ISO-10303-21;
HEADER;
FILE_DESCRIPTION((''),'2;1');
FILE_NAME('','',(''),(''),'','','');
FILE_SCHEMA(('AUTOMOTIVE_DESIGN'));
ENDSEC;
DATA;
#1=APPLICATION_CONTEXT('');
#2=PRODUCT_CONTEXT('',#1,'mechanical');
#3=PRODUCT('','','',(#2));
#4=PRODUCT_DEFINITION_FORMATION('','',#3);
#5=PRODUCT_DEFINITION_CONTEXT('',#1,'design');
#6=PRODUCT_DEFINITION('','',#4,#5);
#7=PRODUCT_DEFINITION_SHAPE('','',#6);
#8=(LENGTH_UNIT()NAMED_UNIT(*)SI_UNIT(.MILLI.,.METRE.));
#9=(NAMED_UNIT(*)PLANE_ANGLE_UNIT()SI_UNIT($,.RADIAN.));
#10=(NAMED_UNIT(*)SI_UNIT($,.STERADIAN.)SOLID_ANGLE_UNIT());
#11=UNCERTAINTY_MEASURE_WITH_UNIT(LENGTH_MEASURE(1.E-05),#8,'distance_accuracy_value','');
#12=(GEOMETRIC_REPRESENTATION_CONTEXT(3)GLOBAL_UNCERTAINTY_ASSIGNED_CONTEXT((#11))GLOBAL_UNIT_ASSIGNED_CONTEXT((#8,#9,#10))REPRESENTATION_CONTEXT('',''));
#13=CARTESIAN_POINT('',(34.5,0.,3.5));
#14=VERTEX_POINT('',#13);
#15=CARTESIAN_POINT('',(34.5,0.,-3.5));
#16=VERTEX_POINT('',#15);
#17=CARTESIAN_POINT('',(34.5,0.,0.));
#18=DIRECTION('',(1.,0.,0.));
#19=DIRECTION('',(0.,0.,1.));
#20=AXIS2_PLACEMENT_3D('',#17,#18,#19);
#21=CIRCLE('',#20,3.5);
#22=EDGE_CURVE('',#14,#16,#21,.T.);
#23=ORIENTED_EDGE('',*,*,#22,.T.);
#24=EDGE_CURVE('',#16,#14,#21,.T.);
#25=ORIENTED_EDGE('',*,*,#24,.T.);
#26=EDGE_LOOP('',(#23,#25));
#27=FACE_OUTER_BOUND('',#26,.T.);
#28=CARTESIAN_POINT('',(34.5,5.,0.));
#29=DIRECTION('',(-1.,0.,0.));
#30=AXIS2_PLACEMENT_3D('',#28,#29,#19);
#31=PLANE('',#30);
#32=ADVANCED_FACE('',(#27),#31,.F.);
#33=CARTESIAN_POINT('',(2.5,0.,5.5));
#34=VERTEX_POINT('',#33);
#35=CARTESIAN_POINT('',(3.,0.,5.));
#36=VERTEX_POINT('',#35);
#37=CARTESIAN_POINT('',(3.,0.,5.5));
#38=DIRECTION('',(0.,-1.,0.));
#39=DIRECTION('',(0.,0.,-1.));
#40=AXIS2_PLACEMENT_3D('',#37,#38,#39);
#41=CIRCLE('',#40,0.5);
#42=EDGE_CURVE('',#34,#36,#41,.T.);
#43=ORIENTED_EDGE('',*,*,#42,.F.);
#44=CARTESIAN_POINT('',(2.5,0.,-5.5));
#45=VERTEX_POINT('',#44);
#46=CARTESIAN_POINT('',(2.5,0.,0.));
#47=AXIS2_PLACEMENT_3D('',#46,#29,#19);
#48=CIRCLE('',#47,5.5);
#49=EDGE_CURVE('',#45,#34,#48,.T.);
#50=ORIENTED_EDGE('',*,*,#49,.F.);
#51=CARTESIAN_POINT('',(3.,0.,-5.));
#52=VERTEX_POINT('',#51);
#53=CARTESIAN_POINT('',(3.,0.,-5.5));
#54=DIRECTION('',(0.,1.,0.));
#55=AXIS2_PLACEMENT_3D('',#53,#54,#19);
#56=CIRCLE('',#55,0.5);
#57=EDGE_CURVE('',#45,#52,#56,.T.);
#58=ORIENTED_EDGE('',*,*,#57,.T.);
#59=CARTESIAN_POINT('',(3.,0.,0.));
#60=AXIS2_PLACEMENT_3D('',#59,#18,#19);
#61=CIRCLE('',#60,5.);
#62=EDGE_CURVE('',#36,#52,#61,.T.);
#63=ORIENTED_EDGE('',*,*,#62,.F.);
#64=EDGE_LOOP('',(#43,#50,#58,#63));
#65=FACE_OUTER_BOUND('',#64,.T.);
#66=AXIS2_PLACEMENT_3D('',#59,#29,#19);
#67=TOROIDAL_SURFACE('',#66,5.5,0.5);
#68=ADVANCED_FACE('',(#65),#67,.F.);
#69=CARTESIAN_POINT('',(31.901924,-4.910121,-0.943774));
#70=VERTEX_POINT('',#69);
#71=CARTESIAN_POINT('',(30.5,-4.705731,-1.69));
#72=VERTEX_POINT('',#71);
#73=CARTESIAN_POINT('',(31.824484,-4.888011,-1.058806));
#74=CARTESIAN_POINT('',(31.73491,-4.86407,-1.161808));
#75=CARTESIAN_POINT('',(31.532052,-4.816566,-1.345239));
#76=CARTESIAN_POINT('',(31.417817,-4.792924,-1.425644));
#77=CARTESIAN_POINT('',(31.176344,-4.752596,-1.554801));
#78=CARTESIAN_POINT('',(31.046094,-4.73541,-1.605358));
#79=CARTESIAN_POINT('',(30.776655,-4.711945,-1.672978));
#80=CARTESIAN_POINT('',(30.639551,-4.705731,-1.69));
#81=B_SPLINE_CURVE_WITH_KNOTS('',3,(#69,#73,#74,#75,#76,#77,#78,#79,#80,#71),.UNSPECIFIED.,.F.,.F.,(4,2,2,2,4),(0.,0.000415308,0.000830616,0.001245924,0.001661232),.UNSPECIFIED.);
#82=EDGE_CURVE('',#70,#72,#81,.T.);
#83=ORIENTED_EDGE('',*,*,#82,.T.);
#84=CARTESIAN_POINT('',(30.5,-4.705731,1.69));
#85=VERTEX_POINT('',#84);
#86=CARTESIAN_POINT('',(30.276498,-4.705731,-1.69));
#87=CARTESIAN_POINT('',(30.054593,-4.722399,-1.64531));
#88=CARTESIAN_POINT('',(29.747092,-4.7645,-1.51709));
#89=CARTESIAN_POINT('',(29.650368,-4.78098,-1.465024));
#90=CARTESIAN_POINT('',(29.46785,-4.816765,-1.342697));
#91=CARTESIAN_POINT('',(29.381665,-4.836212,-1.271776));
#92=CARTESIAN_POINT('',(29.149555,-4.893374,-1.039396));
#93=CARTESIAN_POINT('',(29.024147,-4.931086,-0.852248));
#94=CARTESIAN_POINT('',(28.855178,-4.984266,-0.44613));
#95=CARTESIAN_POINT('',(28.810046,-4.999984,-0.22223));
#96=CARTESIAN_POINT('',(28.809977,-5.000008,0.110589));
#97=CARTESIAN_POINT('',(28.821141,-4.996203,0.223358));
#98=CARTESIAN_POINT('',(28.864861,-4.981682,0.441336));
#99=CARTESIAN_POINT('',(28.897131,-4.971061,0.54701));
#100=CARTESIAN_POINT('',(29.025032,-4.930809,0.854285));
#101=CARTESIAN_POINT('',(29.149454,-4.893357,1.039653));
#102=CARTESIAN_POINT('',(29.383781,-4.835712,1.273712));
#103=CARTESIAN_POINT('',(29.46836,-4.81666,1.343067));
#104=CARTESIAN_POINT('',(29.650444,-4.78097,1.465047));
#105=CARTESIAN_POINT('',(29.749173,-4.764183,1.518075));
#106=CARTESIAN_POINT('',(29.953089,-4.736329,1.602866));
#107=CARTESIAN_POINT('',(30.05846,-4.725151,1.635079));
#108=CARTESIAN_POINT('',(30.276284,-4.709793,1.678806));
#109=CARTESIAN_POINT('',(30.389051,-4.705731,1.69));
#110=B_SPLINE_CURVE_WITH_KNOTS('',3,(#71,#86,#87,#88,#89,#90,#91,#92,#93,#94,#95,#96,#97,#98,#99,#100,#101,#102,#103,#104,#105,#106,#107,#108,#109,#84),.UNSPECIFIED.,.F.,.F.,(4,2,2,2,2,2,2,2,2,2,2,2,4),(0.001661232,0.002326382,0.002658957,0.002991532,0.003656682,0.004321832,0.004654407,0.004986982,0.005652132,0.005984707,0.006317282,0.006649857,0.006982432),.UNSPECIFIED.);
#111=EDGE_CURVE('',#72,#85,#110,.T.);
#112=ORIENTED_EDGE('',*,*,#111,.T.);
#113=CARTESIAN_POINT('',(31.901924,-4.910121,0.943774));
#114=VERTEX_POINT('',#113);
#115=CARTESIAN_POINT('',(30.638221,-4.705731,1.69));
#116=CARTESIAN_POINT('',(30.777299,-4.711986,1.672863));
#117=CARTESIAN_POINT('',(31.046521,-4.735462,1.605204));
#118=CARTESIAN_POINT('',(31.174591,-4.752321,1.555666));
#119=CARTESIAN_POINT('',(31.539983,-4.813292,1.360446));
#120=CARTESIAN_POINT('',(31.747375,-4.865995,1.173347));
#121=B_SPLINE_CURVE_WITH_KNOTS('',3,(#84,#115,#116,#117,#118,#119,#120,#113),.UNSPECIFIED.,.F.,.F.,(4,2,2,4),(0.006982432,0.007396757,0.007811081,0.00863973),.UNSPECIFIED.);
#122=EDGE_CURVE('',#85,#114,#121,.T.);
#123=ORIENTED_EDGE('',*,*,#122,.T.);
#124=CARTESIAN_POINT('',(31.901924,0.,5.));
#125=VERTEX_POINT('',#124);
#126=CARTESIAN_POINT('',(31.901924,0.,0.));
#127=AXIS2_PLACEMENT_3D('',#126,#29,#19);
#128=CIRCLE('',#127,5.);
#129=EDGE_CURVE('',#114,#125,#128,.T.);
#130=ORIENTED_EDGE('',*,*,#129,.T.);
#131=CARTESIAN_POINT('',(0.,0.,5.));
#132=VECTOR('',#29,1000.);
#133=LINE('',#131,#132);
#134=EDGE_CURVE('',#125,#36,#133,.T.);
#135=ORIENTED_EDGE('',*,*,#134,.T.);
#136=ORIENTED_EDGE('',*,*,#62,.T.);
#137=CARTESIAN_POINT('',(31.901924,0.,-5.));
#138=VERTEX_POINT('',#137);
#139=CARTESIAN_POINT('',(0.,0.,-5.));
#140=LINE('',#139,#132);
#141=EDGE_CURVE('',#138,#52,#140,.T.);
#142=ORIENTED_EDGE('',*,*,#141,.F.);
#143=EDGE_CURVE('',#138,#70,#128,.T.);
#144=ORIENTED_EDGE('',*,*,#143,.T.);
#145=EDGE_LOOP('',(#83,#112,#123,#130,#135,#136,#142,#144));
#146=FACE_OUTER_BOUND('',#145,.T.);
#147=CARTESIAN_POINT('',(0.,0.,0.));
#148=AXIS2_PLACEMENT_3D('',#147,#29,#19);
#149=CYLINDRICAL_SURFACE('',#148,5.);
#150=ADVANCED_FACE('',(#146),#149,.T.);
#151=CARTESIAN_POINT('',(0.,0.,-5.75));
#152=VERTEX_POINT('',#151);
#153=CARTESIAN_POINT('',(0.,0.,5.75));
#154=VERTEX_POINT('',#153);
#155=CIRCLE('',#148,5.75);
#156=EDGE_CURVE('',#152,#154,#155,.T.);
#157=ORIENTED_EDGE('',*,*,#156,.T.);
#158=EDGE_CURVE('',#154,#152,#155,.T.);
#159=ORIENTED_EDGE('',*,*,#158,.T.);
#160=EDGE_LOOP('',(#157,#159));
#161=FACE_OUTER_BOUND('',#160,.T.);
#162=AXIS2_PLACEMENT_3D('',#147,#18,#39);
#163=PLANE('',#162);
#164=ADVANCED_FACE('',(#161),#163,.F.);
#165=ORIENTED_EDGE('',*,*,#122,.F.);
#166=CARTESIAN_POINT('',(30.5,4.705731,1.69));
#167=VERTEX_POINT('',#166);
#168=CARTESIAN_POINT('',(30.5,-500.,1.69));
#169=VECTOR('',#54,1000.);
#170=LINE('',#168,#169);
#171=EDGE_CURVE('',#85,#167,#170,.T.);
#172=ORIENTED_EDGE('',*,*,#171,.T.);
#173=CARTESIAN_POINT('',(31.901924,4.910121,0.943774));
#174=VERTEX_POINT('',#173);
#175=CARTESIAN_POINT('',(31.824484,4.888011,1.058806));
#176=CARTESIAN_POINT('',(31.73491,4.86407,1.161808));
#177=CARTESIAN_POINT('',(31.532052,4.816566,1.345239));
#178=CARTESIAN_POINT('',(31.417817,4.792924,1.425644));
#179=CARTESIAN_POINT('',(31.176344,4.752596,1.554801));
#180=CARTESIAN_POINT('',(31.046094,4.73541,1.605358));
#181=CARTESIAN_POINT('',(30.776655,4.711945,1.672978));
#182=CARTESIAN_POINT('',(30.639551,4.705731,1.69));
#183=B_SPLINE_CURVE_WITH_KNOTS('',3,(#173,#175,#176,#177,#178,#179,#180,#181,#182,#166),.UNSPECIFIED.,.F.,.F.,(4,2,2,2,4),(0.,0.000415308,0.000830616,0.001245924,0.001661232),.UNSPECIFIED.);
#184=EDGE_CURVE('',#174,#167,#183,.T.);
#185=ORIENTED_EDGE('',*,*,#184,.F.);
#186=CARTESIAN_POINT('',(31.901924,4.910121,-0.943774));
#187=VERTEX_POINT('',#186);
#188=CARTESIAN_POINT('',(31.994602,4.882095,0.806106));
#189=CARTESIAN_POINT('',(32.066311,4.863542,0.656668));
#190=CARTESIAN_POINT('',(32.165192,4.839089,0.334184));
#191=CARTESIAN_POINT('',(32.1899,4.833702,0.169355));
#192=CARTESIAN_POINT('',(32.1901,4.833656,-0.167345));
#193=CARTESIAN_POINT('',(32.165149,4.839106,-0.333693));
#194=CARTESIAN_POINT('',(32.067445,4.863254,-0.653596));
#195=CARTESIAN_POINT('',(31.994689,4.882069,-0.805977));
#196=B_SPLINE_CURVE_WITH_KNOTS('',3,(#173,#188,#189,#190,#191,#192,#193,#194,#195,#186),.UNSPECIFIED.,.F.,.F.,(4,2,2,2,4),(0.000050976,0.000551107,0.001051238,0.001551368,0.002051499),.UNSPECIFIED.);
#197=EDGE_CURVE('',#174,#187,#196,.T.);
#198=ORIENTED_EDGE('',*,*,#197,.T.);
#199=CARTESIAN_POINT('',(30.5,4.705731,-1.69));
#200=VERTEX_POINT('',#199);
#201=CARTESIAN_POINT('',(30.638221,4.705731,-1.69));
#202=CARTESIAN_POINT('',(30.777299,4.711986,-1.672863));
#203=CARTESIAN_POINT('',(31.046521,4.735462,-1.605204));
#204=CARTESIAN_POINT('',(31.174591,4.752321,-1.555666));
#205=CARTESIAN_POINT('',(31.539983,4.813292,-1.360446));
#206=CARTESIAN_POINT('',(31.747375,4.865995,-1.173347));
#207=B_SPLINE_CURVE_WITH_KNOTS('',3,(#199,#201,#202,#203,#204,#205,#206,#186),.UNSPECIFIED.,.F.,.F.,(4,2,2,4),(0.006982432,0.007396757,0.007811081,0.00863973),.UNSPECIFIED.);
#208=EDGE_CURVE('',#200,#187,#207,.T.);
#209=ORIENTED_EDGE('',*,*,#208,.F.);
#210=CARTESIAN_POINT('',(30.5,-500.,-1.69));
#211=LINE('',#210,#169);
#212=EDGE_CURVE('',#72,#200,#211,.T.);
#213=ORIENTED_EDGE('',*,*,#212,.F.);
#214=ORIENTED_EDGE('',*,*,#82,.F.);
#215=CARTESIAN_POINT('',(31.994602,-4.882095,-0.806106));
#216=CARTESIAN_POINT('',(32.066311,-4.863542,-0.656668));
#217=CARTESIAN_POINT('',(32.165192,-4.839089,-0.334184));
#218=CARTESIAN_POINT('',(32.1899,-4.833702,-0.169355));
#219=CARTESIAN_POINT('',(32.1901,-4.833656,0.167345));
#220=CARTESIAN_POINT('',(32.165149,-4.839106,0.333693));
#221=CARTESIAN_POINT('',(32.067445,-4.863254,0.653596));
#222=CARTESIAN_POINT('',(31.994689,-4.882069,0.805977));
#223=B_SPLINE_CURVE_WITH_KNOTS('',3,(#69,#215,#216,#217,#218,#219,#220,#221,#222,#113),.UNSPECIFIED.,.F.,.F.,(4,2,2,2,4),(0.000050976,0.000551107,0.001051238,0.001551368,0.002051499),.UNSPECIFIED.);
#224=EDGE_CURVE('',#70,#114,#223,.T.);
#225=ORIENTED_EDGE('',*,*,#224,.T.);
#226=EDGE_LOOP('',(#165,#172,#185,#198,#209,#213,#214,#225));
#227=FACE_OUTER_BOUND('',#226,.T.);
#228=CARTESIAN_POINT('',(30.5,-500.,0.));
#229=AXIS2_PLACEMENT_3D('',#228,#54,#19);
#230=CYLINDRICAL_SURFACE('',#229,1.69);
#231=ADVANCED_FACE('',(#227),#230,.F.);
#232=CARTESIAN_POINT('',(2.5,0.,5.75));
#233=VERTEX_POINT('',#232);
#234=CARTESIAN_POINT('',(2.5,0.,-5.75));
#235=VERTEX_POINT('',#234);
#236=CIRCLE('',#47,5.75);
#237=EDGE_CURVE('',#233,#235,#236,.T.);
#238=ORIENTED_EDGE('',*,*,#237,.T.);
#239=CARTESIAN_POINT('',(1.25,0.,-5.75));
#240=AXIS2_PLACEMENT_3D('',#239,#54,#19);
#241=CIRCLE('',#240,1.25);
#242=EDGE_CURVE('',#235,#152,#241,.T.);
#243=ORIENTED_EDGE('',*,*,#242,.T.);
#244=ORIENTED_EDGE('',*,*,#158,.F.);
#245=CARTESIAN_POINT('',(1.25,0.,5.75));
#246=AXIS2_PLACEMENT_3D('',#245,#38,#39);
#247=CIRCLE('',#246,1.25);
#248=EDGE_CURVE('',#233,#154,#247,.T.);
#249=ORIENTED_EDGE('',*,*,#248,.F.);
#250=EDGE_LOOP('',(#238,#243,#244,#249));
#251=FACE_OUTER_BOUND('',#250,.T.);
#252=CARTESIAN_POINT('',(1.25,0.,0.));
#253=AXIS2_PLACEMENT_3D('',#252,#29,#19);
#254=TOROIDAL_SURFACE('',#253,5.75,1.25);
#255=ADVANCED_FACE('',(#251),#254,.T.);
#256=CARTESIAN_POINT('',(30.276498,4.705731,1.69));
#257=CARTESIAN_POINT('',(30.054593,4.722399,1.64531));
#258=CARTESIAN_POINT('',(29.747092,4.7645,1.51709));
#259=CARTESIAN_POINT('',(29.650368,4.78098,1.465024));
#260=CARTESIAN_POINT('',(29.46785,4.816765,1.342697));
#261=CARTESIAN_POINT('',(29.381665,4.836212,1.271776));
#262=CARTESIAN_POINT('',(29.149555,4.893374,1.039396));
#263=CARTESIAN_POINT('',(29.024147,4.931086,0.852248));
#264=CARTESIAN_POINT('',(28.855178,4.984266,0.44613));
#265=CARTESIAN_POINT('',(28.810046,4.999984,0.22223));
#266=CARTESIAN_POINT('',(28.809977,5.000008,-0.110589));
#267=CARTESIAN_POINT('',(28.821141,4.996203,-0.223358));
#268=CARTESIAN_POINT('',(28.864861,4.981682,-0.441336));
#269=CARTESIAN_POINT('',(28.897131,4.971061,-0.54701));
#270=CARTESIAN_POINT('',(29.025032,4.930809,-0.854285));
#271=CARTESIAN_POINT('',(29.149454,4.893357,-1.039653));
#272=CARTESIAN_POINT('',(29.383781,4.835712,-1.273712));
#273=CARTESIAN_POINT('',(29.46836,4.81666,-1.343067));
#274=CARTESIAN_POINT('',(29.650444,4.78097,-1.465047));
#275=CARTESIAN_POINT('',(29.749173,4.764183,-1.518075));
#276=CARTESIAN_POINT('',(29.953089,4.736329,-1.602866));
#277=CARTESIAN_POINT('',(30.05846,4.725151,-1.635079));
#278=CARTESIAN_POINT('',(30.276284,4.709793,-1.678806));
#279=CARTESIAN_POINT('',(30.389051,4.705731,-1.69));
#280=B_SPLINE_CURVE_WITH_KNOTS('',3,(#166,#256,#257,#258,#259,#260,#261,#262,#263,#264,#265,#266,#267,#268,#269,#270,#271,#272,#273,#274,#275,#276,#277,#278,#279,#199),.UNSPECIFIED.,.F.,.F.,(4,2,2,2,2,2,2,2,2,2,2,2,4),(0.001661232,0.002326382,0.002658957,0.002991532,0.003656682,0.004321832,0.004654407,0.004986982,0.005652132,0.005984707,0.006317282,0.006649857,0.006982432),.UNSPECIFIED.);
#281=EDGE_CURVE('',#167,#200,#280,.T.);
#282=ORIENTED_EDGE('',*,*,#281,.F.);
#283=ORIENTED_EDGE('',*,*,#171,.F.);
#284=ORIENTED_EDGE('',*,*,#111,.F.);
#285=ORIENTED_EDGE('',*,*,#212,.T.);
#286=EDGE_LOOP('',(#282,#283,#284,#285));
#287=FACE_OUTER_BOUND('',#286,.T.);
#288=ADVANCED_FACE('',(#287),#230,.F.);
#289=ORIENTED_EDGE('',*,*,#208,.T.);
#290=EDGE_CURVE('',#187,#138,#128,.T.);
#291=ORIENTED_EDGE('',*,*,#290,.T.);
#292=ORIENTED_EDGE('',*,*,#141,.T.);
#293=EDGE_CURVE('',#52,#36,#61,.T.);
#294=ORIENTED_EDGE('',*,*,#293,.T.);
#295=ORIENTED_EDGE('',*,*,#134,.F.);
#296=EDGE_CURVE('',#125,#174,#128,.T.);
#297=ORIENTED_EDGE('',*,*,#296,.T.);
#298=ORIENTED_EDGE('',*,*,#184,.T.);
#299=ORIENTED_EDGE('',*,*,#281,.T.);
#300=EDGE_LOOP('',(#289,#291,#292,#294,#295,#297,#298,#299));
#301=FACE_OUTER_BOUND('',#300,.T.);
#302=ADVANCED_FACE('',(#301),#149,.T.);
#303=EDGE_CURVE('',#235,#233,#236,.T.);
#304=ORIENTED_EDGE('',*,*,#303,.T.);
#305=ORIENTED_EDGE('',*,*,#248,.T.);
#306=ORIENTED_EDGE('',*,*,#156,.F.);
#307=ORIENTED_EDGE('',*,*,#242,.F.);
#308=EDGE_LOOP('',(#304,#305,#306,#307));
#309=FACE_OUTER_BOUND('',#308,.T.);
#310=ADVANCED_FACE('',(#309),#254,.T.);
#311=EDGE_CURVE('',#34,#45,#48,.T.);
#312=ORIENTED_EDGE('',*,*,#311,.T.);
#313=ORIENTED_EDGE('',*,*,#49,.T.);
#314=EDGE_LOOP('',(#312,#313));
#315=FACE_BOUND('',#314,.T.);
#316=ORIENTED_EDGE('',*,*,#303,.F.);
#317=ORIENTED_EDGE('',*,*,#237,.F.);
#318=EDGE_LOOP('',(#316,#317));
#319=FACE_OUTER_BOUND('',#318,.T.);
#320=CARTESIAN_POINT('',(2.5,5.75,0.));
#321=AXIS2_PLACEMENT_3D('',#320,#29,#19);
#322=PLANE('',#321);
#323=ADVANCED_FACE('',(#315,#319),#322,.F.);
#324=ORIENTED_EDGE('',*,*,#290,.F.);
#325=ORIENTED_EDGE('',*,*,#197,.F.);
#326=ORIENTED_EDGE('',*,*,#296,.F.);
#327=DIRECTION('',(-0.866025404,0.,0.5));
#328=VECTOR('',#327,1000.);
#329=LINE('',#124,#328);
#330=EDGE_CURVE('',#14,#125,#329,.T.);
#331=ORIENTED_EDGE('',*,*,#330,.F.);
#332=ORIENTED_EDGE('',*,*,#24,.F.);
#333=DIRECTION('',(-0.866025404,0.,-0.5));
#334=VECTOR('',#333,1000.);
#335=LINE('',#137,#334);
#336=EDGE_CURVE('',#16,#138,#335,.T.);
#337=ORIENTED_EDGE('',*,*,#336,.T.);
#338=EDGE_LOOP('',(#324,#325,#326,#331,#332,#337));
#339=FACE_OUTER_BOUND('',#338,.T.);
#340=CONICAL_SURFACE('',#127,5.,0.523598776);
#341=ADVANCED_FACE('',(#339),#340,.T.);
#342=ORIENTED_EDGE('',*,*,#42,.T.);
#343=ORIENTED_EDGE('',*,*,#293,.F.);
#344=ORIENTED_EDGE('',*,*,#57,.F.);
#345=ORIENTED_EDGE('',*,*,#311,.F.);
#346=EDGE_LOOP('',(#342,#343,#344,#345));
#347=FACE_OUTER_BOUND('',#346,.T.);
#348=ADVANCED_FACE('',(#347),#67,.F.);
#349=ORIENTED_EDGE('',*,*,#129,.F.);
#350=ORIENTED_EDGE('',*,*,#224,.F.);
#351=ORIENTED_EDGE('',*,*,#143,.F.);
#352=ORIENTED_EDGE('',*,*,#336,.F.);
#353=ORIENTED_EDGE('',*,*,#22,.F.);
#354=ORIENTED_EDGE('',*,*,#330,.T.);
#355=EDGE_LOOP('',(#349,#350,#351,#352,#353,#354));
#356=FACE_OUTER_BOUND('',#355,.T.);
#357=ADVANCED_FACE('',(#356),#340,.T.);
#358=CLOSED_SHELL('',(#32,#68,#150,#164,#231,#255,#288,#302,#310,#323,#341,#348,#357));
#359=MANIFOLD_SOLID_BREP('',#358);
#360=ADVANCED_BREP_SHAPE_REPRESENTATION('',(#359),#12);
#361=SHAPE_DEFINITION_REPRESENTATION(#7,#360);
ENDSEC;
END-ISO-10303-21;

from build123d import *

# Parameters (mm, degrees)
FILLET_1_R          = 0.5
CHAMFER_1_SIZE      = 2.598076211
CHAMFER_1_SIZE2     = 1.5
SKETCH_2_R          = 1.69
CUT_EXTRUDE_1_DEPTH = 500


with BuildPart() as part:
    # 草图1 → Revolve 730 (revolve)
    with BuildSketch(Plane.XY, mode=Mode.PRIVATE) as revolve_730_sk:
        with BuildLine():
            Line((0, 0), (34.5, 0))
            Line((34.5, 0), (34.5, 5))
            Line((34.5, 5), (2.5, 5))
            Line((2.5, 5), (2.5, 5.75))
            ThreePointArc((2.5, 5.75), (1.25, 7), (0, 5.75))
            Line((0, 5.75), (0, 0))
        make_face()
    revolve(revolve_730_sk.sketch.rotate(Axis((0, 0, 0), (1, 0, 0)), 90), axis=Axis((0, 0, 0), (1, 0, 0)))

    # 圆角1
    fillet_1_edges = [part.edges().sort_by_distance(p)[0] for p in [
        (2.5, 0, -5),
    ]]
    fillet(fillet_1_edges, radius=FILLET_1_R)

    # 倒角1
    chamfer_1_edges = [part.edges().sort_by_distance(p)[0] for p in [
        (34.5, 0, -5),
    ]]
    chamfer_1_side = [part.faces().sort_by_distance(p)[0] for p in [
        (18.75, 0, -5),
    ]]
    chamfer(chamfer_1_edges, length=CHAMFER_1_SIZE, length2=CHAMFER_1_SIZE2, reference=chamfer_1_side[0])

    # 草图2 → 切除-拉伸1 (cut, symmetric)
    with BuildSketch(Plane(origin=(0, 0, 0), x_dir=(1, 0, 0), z_dir=(0, 1, 0))):
        with Locations(Location((30.5, 0, 0), (0, 0, 326.051586003))):
            Circle(SKETCH_2_R)
    extrude(amount=CUT_EXTRUDE_1_DEPTH, both=True, mode=Mode.SUBTRACT)


solid = part.part
